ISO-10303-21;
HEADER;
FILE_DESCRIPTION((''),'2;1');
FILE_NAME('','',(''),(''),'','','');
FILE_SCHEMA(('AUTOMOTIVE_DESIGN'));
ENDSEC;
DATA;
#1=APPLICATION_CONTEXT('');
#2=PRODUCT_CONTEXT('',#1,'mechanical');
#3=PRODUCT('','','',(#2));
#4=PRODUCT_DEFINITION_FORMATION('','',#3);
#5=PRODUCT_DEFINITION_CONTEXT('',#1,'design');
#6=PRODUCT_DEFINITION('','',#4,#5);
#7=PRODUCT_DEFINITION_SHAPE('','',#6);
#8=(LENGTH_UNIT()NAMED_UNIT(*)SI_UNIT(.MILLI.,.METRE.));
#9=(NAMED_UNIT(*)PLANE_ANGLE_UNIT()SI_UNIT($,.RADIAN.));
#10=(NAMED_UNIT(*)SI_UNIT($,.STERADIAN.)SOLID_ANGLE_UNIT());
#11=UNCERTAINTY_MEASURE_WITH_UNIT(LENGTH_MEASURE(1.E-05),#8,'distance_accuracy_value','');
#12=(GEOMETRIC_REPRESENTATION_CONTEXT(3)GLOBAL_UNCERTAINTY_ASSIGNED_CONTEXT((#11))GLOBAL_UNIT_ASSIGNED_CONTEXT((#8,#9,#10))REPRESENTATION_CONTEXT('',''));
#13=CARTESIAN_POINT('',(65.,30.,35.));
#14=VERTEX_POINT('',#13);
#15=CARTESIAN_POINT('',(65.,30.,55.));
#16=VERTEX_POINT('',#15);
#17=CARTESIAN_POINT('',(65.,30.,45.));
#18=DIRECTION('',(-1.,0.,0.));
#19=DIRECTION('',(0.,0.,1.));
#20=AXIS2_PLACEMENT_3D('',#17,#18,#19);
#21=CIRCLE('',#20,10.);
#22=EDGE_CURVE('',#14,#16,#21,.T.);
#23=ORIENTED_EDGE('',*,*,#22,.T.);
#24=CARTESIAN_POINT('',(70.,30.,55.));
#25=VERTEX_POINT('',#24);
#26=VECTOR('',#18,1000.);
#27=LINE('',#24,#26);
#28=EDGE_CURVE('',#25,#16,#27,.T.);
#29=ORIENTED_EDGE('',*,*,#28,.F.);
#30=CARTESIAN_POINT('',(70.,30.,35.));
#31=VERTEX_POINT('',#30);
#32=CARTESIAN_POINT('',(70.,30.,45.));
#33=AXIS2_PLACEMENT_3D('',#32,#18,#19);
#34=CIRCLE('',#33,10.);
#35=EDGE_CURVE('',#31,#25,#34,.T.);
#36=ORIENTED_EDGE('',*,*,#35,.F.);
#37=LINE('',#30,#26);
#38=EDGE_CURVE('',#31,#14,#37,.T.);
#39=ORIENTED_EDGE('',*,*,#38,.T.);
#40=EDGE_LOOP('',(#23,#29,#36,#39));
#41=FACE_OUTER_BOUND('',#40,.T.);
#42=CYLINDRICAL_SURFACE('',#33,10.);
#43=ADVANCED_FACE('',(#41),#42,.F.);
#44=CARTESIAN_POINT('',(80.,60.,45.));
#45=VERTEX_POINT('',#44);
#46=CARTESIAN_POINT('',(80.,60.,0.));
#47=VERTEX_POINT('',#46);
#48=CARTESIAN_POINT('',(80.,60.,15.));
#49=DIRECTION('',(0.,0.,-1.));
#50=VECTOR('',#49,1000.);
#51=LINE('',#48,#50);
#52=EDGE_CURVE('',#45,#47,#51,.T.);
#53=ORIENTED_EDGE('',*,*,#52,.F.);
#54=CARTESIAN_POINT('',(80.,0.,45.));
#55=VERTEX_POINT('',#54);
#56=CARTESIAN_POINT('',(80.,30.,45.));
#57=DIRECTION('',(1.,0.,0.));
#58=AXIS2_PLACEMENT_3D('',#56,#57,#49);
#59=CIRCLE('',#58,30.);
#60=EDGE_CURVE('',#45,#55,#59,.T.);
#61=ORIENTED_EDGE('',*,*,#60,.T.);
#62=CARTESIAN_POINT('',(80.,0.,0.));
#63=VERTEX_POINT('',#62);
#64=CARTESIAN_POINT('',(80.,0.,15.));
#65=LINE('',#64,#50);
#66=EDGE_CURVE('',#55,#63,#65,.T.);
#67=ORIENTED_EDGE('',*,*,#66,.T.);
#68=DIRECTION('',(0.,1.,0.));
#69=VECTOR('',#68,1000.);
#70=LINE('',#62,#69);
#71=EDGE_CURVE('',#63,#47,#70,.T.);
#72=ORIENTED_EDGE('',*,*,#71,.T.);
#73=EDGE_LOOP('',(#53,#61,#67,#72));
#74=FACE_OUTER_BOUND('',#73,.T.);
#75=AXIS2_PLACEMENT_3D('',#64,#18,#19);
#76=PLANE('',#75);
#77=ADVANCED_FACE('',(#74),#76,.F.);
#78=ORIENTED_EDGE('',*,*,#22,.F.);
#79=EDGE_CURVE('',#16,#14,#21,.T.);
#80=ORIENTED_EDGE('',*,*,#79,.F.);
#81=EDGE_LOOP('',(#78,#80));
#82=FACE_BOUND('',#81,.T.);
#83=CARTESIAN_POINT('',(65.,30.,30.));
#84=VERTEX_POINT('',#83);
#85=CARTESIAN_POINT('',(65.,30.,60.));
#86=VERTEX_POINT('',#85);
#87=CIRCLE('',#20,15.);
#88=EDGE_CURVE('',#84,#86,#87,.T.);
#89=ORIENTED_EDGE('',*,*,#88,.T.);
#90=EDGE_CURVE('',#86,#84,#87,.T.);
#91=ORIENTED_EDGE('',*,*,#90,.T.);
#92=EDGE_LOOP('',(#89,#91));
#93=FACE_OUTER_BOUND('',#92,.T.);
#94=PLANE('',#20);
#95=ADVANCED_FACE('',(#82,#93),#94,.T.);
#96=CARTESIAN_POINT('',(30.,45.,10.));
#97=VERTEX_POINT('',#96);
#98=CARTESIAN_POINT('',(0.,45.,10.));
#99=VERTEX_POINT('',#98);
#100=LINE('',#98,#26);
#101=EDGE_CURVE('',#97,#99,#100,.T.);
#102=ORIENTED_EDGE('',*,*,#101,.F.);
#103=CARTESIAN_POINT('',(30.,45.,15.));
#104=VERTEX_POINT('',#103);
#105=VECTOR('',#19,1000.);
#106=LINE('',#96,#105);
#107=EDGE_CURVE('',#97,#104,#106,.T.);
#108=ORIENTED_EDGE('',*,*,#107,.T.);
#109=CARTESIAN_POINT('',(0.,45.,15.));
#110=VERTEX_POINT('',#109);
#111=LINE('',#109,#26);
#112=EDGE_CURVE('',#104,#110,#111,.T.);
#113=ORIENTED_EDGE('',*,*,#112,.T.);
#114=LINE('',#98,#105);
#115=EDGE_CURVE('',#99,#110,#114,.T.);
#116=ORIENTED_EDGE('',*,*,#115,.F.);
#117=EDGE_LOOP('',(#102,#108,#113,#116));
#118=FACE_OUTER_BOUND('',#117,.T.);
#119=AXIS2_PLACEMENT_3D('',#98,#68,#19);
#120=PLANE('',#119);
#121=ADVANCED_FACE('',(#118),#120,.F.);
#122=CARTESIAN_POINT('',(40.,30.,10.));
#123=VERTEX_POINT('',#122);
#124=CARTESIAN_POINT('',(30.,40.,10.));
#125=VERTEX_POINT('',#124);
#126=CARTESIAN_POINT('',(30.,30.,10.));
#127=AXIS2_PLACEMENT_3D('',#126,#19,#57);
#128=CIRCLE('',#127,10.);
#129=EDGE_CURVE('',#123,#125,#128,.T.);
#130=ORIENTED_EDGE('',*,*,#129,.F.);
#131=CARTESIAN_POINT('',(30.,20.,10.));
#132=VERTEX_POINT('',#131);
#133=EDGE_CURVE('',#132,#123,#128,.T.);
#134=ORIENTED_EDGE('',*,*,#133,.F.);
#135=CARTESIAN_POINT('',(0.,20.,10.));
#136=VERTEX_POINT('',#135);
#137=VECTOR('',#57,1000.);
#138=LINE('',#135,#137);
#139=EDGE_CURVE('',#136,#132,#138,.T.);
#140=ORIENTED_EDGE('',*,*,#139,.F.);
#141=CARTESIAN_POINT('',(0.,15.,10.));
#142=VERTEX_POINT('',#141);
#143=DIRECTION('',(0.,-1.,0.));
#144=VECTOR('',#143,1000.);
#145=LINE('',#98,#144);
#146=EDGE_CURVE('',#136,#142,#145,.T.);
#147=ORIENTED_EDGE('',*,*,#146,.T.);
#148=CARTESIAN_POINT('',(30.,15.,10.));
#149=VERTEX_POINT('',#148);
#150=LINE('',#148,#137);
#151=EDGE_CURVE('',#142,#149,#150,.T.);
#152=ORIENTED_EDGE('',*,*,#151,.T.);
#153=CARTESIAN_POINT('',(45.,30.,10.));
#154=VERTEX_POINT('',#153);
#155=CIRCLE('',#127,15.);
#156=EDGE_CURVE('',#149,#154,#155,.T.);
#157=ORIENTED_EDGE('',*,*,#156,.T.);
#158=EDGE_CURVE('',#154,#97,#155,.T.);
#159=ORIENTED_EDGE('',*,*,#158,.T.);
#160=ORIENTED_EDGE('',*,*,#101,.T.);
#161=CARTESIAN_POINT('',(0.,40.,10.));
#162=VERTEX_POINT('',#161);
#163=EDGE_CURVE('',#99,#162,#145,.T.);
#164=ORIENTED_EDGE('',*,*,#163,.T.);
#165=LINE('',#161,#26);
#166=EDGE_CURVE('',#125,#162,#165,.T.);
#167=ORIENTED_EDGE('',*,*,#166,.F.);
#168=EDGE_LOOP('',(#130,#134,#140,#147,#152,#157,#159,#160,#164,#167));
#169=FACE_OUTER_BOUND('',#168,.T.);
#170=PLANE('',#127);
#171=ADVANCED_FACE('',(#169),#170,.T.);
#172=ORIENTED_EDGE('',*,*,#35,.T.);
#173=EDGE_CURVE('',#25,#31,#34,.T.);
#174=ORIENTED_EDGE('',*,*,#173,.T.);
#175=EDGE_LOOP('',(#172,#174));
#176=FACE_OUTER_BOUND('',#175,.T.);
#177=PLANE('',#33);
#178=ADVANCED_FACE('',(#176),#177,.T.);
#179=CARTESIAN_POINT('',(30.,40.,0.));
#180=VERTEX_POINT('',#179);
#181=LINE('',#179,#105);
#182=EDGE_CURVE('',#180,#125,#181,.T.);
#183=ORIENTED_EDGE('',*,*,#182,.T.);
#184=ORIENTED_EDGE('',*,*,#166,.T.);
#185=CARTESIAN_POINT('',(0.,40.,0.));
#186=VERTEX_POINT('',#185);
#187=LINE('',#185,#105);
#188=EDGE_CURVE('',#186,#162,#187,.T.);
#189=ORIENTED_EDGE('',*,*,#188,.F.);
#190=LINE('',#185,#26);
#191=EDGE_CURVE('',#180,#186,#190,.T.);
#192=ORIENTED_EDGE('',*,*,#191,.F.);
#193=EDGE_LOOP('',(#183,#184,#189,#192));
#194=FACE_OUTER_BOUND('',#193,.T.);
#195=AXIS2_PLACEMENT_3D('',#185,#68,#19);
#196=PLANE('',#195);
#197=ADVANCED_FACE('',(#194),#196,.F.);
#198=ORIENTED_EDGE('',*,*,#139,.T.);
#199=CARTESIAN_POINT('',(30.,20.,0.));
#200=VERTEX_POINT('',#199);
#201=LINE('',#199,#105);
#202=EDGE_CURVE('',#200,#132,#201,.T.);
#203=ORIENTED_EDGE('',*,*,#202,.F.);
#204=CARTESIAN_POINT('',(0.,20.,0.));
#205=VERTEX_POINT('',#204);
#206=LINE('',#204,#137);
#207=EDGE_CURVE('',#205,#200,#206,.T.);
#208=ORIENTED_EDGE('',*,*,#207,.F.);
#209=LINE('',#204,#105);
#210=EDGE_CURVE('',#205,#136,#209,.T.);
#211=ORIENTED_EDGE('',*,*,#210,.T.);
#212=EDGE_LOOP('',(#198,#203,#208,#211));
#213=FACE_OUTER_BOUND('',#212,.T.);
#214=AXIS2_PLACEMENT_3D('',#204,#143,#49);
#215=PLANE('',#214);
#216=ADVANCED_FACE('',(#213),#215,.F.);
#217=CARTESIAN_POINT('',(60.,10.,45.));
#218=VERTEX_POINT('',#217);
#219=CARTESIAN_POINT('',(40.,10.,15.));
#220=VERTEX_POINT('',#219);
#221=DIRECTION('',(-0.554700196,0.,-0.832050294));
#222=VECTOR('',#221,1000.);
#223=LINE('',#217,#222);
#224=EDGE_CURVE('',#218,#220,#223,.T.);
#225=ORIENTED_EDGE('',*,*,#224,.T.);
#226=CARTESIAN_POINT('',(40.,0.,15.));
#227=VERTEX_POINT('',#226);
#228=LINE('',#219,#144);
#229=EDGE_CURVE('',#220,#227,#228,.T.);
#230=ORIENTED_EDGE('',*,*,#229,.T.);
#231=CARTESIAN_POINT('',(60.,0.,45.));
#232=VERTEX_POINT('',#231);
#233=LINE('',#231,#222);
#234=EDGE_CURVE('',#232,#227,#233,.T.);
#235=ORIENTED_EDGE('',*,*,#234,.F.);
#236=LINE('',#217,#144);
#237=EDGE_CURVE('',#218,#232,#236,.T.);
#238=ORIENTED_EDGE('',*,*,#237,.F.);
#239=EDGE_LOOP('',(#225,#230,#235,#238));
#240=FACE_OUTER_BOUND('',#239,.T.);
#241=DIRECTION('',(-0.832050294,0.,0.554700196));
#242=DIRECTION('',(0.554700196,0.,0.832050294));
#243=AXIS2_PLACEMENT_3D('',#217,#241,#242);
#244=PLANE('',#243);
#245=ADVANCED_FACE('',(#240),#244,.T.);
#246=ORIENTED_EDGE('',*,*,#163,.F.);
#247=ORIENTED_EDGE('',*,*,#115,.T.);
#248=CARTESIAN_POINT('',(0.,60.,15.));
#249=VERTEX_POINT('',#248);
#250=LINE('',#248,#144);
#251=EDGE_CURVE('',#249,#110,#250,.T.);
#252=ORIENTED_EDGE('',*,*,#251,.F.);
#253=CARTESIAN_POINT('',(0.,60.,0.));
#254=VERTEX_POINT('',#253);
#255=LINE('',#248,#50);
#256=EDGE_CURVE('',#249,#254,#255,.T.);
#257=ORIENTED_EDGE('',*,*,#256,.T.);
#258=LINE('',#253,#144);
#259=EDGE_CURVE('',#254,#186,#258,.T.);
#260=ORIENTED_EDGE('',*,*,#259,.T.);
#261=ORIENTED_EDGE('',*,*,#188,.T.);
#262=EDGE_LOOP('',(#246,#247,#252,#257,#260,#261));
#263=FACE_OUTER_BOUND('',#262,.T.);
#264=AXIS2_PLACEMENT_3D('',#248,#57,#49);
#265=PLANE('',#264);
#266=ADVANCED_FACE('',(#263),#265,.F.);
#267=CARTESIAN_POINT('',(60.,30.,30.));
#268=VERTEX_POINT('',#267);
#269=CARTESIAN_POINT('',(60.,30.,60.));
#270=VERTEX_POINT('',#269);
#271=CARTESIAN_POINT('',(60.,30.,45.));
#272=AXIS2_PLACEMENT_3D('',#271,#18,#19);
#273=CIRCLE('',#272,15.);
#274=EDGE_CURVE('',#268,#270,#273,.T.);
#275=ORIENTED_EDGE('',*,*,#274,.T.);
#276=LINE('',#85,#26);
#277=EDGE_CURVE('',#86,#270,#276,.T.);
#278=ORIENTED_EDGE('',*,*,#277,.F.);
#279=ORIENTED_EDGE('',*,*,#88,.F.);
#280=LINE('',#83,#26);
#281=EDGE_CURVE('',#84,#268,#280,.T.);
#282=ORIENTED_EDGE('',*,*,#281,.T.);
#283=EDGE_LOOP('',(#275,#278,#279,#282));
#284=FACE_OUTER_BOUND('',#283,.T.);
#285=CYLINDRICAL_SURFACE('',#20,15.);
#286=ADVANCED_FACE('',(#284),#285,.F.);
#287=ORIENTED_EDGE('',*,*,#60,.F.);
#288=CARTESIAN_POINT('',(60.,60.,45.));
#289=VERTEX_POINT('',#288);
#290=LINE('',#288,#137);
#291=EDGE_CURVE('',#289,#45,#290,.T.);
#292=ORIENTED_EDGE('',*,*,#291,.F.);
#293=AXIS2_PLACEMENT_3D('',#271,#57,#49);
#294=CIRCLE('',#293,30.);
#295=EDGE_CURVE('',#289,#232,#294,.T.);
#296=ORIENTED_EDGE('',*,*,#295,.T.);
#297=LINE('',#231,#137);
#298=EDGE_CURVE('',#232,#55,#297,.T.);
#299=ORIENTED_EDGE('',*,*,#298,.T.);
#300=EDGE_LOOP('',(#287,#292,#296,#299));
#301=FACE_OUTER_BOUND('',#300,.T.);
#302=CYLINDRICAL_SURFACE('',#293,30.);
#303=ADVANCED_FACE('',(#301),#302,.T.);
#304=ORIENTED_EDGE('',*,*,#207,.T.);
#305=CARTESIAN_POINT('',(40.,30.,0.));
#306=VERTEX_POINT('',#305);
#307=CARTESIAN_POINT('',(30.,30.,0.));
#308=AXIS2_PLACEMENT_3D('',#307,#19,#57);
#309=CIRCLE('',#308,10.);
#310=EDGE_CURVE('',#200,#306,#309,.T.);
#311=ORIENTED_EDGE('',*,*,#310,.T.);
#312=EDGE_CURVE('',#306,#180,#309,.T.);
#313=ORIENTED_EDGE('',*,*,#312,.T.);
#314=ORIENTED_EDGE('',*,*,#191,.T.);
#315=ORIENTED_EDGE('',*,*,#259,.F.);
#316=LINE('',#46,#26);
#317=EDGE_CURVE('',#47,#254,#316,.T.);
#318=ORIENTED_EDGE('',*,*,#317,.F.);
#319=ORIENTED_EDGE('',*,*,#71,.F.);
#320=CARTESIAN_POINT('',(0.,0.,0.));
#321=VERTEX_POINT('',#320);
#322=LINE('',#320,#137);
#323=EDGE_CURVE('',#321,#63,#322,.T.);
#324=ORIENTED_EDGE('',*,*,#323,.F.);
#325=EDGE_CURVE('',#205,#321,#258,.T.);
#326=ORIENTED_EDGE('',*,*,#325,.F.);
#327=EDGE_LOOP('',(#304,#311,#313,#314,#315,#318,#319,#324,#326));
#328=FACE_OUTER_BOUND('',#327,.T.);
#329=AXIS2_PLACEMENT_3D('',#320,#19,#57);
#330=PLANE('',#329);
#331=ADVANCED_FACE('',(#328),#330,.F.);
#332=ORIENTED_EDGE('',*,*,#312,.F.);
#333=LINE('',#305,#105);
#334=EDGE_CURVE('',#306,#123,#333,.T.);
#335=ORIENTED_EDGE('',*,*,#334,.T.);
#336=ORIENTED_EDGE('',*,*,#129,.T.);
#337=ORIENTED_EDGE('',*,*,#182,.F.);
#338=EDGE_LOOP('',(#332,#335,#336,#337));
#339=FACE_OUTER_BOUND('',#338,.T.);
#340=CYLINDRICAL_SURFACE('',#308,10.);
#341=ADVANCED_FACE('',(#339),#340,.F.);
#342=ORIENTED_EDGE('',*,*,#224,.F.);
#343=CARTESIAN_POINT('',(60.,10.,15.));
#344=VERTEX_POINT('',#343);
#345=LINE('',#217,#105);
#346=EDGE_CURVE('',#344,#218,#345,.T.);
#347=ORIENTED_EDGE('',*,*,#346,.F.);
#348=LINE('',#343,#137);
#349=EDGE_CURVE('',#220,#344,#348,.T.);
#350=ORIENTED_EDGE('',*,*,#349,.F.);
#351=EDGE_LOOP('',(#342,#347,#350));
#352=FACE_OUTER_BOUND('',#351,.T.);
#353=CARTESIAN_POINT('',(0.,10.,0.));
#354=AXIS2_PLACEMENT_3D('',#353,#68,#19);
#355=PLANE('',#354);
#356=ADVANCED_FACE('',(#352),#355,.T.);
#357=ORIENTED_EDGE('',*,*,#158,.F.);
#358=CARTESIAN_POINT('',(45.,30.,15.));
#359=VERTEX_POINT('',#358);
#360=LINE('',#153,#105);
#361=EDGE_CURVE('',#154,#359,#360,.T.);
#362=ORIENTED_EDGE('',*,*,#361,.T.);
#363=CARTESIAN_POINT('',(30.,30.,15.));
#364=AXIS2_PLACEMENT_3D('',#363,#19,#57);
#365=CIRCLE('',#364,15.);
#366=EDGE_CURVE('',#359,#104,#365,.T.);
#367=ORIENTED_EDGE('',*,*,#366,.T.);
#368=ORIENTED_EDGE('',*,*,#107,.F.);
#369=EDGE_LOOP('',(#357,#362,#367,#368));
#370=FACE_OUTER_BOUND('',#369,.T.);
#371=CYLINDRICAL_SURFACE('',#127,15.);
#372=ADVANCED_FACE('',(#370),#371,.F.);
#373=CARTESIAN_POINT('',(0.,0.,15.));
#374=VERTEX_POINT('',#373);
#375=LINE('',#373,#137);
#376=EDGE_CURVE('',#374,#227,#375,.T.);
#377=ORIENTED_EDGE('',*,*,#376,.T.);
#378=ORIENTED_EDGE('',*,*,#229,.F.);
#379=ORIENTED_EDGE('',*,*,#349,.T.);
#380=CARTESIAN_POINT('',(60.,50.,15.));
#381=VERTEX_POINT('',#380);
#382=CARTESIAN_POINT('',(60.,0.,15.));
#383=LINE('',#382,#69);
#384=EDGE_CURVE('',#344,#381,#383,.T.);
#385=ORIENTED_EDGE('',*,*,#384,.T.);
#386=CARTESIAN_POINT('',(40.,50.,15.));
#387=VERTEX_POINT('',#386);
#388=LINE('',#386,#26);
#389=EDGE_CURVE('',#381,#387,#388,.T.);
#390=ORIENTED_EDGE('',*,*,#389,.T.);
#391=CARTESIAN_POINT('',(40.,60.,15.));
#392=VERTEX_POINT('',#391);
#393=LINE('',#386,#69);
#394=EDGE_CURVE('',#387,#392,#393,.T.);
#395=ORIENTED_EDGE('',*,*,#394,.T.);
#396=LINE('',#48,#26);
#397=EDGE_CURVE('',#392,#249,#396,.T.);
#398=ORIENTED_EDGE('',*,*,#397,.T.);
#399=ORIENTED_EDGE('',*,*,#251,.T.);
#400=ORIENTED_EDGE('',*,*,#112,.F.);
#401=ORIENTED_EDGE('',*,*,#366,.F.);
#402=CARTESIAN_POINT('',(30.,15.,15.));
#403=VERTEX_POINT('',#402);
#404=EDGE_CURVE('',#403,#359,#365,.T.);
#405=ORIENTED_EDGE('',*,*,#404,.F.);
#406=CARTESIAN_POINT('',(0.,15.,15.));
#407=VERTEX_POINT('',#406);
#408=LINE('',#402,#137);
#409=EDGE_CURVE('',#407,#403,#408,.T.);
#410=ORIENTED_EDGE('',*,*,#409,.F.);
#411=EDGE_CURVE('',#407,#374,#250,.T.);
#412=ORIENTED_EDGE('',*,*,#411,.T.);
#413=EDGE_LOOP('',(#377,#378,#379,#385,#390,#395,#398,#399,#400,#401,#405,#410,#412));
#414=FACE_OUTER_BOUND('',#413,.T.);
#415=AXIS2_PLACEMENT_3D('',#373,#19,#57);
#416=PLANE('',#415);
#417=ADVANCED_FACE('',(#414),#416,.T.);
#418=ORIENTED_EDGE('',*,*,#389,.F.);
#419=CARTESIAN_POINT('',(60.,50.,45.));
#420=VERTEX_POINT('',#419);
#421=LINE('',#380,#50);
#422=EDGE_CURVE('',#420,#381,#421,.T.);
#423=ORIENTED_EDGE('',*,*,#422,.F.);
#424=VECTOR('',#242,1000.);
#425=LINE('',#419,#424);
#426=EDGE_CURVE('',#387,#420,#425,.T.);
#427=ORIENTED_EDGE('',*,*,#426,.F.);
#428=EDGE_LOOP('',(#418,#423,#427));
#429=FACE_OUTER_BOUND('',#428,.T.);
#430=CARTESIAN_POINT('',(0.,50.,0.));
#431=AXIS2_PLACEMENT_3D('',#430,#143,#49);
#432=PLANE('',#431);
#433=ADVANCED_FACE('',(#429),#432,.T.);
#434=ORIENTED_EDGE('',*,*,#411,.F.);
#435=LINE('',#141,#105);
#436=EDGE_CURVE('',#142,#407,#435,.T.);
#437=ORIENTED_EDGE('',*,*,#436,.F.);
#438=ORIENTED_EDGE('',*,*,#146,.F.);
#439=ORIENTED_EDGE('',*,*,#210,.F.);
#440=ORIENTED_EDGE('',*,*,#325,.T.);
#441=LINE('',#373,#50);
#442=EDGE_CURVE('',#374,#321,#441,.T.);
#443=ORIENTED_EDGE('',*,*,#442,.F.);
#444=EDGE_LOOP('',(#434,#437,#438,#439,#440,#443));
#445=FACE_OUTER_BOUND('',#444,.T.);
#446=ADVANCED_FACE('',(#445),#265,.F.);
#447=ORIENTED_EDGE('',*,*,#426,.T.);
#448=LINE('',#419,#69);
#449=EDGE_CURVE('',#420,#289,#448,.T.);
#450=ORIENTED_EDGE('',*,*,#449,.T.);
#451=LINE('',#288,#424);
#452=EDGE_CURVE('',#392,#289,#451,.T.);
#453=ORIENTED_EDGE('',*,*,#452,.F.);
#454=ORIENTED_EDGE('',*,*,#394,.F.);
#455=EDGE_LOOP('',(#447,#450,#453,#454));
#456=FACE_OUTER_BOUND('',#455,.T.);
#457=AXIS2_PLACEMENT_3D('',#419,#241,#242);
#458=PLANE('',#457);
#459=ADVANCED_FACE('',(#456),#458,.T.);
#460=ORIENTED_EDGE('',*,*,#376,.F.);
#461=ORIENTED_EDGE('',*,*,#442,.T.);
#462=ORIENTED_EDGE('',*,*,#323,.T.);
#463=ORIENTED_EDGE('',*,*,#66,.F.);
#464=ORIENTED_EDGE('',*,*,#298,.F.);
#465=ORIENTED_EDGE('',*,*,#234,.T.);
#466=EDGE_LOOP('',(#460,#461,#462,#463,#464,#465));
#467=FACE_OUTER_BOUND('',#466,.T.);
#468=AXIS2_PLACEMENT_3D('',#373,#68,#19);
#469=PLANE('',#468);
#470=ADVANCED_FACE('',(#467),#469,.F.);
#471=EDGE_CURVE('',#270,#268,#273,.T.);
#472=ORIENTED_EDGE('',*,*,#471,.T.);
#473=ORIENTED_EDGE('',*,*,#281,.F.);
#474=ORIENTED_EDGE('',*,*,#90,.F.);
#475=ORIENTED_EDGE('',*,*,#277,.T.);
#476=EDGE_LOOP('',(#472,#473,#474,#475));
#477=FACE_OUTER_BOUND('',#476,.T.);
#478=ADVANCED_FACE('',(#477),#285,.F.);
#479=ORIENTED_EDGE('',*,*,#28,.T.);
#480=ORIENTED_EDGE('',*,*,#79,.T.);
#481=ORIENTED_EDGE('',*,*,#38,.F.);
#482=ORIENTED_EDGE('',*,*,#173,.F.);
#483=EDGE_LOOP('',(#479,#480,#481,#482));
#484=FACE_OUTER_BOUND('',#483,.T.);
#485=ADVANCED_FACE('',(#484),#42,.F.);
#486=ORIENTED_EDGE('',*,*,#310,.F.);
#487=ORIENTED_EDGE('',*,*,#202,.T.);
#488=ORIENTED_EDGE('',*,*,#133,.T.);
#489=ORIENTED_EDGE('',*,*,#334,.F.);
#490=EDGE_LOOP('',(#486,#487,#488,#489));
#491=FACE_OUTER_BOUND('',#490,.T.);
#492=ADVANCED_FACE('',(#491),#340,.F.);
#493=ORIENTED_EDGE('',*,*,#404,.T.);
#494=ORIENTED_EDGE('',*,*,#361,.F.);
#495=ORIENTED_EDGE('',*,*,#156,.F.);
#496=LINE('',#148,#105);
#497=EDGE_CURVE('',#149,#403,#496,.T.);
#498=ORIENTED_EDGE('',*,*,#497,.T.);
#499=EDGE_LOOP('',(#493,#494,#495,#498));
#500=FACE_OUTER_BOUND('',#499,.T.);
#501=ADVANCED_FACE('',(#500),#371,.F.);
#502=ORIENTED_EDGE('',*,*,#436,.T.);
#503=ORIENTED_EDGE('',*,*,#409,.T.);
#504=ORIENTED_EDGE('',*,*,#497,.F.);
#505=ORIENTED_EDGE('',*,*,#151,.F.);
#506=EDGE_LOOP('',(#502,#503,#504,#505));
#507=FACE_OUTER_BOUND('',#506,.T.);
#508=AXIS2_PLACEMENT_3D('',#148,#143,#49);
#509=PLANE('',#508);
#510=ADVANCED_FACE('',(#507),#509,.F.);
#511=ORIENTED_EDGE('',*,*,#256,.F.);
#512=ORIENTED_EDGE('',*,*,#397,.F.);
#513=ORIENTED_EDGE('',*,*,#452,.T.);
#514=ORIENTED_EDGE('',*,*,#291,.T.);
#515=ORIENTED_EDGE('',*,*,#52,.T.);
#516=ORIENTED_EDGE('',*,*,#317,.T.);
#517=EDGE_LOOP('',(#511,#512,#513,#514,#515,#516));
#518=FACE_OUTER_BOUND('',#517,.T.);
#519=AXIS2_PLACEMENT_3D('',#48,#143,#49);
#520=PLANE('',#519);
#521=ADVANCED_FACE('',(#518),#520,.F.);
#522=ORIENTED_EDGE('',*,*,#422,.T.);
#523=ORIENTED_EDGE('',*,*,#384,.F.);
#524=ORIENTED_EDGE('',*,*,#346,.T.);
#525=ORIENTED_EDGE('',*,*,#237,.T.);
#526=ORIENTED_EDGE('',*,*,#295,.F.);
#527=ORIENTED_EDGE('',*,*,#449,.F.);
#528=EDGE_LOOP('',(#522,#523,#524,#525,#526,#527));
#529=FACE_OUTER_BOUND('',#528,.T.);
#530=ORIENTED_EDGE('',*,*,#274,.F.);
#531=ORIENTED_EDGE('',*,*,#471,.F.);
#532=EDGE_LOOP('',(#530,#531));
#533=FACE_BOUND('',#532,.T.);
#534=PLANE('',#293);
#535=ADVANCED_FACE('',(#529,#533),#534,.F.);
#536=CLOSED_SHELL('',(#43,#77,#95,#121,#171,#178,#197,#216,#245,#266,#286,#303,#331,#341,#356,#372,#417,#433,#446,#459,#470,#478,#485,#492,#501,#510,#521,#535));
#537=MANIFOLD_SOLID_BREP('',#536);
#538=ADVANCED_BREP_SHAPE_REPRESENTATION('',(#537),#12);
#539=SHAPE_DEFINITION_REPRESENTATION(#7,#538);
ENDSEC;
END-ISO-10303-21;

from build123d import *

# Parameters (mm, degrees)
BASE_PLATE_SKETCH_W = 80
BASE_PLATE_SKETCH_H = 60
BASE_PLATE_DEPTH    = 15
UPRIGHT_BLOCK_DEPTH = 20
RECESS_30_SKETCH_R  = 15
RECESS_30_DEPTH     = 5
RECESS_20_SKETCH_R  = 10
RECESS_20_DEPTH     = 5
SLOT_30_DEPTH       = 5
SLOT_STEP_20_DEPTH  = 10
SIDE_BOSS_DEPTH     = 10
ROUNDED_BOSS_DEPTH  = 10


with BuildPart() as part:
    # Base Plate Sketch → Base Plate (new body)
    with BuildSketch(Plane.XY):
        with Locations((40, 30)):
            Rectangle(BASE_PLATE_SKETCH_W, BASE_PLATE_SKETCH_H)
    extrude(amount=BASE_PLATE_DEPTH)

    # Upright Block Sketch → Upright Block (add)
    with BuildSketch(Plane(origin=(80, 0, 0), x_dir=(0, 0, -1), z_dir=(1, 0, 0))):
        with BuildLine():
            Line((-15, 60), (-45, 60))
            ThreePointArc((-45, 60), (-75, 30), (-45, 0))
            Line((-45, 0), (-15, 0))
            Line((-15, 0), (-15, 60))
        make_face()
    extrude(amount=-UPRIGHT_BLOCK_DEPTH)

    # Recess Ø30 Sketch → Recess Ø30 (cut)
    with BuildSketch(Plane.ZY.offset(-60)):
        with Locations((45, 30)):
            Circle(RECESS_30_SKETCH_R)
    extrude(amount=-RECESS_30_DEPTH, mode=Mode.SUBTRACT)

    # Recess Ø20 Sketch → Recess Ø20 (cut)
    with BuildSketch(Plane.ZY.offset(-65)):
        with Locations((45, 30)):
            Circle(RECESS_20_SKETCH_R)
    extrude(amount=-RECESS_20_DEPTH, mode=Mode.SUBTRACT)

    # Slot 30 Sketch → Slot 30 (cut)
    with BuildSketch(Plane.XY.offset(15)):
        with BuildLine():
            Line((0, 45), (0, 15))
            Line((0, 15), (30, 15))
            ThreePointArc((30, 15), (45, 30), (30, 45))
            Line((30, 45), (0, 45))
        make_face()
    extrude(amount=-SLOT_30_DEPTH, mode=Mode.SUBTRACT)

    # Slot Step 20 Sketch → Slot Step 20 (cut)
    with BuildSketch(Plane.XY.offset(10)):
        with BuildLine():
            Line((0, 40), (30, 40))
            ThreePointArc((30, 40), (40, 30), (30, 20))
            Line((30, 20), (0, 20))
            Line((0, 20), (0, 40))
        make_face()
    extrude(amount=-SLOT_STEP_20_DEPTH, mode=Mode.SUBTRACT)

    # Side Boss Sketch → Side Boss (add)
    with BuildSketch(Plane.XZ):
        Polygon((60, 45), (40, 15), (60, 15), align=None)
    extrude(amount=-SIDE_BOSS_DEPTH)

    # Rounded Boss Sketch → Rounded Boss (add)
    with BuildSketch(Plane(origin=(0, 60, 0), x_dir=(1, 0, 0), z_dir=(0, 1, 0))):
        Polygon((40, -15), (60, -15), (60, -45), align=None)
    extrude(amount=-ROUNDED_BOSS_DEPTH)


solid = part.part
